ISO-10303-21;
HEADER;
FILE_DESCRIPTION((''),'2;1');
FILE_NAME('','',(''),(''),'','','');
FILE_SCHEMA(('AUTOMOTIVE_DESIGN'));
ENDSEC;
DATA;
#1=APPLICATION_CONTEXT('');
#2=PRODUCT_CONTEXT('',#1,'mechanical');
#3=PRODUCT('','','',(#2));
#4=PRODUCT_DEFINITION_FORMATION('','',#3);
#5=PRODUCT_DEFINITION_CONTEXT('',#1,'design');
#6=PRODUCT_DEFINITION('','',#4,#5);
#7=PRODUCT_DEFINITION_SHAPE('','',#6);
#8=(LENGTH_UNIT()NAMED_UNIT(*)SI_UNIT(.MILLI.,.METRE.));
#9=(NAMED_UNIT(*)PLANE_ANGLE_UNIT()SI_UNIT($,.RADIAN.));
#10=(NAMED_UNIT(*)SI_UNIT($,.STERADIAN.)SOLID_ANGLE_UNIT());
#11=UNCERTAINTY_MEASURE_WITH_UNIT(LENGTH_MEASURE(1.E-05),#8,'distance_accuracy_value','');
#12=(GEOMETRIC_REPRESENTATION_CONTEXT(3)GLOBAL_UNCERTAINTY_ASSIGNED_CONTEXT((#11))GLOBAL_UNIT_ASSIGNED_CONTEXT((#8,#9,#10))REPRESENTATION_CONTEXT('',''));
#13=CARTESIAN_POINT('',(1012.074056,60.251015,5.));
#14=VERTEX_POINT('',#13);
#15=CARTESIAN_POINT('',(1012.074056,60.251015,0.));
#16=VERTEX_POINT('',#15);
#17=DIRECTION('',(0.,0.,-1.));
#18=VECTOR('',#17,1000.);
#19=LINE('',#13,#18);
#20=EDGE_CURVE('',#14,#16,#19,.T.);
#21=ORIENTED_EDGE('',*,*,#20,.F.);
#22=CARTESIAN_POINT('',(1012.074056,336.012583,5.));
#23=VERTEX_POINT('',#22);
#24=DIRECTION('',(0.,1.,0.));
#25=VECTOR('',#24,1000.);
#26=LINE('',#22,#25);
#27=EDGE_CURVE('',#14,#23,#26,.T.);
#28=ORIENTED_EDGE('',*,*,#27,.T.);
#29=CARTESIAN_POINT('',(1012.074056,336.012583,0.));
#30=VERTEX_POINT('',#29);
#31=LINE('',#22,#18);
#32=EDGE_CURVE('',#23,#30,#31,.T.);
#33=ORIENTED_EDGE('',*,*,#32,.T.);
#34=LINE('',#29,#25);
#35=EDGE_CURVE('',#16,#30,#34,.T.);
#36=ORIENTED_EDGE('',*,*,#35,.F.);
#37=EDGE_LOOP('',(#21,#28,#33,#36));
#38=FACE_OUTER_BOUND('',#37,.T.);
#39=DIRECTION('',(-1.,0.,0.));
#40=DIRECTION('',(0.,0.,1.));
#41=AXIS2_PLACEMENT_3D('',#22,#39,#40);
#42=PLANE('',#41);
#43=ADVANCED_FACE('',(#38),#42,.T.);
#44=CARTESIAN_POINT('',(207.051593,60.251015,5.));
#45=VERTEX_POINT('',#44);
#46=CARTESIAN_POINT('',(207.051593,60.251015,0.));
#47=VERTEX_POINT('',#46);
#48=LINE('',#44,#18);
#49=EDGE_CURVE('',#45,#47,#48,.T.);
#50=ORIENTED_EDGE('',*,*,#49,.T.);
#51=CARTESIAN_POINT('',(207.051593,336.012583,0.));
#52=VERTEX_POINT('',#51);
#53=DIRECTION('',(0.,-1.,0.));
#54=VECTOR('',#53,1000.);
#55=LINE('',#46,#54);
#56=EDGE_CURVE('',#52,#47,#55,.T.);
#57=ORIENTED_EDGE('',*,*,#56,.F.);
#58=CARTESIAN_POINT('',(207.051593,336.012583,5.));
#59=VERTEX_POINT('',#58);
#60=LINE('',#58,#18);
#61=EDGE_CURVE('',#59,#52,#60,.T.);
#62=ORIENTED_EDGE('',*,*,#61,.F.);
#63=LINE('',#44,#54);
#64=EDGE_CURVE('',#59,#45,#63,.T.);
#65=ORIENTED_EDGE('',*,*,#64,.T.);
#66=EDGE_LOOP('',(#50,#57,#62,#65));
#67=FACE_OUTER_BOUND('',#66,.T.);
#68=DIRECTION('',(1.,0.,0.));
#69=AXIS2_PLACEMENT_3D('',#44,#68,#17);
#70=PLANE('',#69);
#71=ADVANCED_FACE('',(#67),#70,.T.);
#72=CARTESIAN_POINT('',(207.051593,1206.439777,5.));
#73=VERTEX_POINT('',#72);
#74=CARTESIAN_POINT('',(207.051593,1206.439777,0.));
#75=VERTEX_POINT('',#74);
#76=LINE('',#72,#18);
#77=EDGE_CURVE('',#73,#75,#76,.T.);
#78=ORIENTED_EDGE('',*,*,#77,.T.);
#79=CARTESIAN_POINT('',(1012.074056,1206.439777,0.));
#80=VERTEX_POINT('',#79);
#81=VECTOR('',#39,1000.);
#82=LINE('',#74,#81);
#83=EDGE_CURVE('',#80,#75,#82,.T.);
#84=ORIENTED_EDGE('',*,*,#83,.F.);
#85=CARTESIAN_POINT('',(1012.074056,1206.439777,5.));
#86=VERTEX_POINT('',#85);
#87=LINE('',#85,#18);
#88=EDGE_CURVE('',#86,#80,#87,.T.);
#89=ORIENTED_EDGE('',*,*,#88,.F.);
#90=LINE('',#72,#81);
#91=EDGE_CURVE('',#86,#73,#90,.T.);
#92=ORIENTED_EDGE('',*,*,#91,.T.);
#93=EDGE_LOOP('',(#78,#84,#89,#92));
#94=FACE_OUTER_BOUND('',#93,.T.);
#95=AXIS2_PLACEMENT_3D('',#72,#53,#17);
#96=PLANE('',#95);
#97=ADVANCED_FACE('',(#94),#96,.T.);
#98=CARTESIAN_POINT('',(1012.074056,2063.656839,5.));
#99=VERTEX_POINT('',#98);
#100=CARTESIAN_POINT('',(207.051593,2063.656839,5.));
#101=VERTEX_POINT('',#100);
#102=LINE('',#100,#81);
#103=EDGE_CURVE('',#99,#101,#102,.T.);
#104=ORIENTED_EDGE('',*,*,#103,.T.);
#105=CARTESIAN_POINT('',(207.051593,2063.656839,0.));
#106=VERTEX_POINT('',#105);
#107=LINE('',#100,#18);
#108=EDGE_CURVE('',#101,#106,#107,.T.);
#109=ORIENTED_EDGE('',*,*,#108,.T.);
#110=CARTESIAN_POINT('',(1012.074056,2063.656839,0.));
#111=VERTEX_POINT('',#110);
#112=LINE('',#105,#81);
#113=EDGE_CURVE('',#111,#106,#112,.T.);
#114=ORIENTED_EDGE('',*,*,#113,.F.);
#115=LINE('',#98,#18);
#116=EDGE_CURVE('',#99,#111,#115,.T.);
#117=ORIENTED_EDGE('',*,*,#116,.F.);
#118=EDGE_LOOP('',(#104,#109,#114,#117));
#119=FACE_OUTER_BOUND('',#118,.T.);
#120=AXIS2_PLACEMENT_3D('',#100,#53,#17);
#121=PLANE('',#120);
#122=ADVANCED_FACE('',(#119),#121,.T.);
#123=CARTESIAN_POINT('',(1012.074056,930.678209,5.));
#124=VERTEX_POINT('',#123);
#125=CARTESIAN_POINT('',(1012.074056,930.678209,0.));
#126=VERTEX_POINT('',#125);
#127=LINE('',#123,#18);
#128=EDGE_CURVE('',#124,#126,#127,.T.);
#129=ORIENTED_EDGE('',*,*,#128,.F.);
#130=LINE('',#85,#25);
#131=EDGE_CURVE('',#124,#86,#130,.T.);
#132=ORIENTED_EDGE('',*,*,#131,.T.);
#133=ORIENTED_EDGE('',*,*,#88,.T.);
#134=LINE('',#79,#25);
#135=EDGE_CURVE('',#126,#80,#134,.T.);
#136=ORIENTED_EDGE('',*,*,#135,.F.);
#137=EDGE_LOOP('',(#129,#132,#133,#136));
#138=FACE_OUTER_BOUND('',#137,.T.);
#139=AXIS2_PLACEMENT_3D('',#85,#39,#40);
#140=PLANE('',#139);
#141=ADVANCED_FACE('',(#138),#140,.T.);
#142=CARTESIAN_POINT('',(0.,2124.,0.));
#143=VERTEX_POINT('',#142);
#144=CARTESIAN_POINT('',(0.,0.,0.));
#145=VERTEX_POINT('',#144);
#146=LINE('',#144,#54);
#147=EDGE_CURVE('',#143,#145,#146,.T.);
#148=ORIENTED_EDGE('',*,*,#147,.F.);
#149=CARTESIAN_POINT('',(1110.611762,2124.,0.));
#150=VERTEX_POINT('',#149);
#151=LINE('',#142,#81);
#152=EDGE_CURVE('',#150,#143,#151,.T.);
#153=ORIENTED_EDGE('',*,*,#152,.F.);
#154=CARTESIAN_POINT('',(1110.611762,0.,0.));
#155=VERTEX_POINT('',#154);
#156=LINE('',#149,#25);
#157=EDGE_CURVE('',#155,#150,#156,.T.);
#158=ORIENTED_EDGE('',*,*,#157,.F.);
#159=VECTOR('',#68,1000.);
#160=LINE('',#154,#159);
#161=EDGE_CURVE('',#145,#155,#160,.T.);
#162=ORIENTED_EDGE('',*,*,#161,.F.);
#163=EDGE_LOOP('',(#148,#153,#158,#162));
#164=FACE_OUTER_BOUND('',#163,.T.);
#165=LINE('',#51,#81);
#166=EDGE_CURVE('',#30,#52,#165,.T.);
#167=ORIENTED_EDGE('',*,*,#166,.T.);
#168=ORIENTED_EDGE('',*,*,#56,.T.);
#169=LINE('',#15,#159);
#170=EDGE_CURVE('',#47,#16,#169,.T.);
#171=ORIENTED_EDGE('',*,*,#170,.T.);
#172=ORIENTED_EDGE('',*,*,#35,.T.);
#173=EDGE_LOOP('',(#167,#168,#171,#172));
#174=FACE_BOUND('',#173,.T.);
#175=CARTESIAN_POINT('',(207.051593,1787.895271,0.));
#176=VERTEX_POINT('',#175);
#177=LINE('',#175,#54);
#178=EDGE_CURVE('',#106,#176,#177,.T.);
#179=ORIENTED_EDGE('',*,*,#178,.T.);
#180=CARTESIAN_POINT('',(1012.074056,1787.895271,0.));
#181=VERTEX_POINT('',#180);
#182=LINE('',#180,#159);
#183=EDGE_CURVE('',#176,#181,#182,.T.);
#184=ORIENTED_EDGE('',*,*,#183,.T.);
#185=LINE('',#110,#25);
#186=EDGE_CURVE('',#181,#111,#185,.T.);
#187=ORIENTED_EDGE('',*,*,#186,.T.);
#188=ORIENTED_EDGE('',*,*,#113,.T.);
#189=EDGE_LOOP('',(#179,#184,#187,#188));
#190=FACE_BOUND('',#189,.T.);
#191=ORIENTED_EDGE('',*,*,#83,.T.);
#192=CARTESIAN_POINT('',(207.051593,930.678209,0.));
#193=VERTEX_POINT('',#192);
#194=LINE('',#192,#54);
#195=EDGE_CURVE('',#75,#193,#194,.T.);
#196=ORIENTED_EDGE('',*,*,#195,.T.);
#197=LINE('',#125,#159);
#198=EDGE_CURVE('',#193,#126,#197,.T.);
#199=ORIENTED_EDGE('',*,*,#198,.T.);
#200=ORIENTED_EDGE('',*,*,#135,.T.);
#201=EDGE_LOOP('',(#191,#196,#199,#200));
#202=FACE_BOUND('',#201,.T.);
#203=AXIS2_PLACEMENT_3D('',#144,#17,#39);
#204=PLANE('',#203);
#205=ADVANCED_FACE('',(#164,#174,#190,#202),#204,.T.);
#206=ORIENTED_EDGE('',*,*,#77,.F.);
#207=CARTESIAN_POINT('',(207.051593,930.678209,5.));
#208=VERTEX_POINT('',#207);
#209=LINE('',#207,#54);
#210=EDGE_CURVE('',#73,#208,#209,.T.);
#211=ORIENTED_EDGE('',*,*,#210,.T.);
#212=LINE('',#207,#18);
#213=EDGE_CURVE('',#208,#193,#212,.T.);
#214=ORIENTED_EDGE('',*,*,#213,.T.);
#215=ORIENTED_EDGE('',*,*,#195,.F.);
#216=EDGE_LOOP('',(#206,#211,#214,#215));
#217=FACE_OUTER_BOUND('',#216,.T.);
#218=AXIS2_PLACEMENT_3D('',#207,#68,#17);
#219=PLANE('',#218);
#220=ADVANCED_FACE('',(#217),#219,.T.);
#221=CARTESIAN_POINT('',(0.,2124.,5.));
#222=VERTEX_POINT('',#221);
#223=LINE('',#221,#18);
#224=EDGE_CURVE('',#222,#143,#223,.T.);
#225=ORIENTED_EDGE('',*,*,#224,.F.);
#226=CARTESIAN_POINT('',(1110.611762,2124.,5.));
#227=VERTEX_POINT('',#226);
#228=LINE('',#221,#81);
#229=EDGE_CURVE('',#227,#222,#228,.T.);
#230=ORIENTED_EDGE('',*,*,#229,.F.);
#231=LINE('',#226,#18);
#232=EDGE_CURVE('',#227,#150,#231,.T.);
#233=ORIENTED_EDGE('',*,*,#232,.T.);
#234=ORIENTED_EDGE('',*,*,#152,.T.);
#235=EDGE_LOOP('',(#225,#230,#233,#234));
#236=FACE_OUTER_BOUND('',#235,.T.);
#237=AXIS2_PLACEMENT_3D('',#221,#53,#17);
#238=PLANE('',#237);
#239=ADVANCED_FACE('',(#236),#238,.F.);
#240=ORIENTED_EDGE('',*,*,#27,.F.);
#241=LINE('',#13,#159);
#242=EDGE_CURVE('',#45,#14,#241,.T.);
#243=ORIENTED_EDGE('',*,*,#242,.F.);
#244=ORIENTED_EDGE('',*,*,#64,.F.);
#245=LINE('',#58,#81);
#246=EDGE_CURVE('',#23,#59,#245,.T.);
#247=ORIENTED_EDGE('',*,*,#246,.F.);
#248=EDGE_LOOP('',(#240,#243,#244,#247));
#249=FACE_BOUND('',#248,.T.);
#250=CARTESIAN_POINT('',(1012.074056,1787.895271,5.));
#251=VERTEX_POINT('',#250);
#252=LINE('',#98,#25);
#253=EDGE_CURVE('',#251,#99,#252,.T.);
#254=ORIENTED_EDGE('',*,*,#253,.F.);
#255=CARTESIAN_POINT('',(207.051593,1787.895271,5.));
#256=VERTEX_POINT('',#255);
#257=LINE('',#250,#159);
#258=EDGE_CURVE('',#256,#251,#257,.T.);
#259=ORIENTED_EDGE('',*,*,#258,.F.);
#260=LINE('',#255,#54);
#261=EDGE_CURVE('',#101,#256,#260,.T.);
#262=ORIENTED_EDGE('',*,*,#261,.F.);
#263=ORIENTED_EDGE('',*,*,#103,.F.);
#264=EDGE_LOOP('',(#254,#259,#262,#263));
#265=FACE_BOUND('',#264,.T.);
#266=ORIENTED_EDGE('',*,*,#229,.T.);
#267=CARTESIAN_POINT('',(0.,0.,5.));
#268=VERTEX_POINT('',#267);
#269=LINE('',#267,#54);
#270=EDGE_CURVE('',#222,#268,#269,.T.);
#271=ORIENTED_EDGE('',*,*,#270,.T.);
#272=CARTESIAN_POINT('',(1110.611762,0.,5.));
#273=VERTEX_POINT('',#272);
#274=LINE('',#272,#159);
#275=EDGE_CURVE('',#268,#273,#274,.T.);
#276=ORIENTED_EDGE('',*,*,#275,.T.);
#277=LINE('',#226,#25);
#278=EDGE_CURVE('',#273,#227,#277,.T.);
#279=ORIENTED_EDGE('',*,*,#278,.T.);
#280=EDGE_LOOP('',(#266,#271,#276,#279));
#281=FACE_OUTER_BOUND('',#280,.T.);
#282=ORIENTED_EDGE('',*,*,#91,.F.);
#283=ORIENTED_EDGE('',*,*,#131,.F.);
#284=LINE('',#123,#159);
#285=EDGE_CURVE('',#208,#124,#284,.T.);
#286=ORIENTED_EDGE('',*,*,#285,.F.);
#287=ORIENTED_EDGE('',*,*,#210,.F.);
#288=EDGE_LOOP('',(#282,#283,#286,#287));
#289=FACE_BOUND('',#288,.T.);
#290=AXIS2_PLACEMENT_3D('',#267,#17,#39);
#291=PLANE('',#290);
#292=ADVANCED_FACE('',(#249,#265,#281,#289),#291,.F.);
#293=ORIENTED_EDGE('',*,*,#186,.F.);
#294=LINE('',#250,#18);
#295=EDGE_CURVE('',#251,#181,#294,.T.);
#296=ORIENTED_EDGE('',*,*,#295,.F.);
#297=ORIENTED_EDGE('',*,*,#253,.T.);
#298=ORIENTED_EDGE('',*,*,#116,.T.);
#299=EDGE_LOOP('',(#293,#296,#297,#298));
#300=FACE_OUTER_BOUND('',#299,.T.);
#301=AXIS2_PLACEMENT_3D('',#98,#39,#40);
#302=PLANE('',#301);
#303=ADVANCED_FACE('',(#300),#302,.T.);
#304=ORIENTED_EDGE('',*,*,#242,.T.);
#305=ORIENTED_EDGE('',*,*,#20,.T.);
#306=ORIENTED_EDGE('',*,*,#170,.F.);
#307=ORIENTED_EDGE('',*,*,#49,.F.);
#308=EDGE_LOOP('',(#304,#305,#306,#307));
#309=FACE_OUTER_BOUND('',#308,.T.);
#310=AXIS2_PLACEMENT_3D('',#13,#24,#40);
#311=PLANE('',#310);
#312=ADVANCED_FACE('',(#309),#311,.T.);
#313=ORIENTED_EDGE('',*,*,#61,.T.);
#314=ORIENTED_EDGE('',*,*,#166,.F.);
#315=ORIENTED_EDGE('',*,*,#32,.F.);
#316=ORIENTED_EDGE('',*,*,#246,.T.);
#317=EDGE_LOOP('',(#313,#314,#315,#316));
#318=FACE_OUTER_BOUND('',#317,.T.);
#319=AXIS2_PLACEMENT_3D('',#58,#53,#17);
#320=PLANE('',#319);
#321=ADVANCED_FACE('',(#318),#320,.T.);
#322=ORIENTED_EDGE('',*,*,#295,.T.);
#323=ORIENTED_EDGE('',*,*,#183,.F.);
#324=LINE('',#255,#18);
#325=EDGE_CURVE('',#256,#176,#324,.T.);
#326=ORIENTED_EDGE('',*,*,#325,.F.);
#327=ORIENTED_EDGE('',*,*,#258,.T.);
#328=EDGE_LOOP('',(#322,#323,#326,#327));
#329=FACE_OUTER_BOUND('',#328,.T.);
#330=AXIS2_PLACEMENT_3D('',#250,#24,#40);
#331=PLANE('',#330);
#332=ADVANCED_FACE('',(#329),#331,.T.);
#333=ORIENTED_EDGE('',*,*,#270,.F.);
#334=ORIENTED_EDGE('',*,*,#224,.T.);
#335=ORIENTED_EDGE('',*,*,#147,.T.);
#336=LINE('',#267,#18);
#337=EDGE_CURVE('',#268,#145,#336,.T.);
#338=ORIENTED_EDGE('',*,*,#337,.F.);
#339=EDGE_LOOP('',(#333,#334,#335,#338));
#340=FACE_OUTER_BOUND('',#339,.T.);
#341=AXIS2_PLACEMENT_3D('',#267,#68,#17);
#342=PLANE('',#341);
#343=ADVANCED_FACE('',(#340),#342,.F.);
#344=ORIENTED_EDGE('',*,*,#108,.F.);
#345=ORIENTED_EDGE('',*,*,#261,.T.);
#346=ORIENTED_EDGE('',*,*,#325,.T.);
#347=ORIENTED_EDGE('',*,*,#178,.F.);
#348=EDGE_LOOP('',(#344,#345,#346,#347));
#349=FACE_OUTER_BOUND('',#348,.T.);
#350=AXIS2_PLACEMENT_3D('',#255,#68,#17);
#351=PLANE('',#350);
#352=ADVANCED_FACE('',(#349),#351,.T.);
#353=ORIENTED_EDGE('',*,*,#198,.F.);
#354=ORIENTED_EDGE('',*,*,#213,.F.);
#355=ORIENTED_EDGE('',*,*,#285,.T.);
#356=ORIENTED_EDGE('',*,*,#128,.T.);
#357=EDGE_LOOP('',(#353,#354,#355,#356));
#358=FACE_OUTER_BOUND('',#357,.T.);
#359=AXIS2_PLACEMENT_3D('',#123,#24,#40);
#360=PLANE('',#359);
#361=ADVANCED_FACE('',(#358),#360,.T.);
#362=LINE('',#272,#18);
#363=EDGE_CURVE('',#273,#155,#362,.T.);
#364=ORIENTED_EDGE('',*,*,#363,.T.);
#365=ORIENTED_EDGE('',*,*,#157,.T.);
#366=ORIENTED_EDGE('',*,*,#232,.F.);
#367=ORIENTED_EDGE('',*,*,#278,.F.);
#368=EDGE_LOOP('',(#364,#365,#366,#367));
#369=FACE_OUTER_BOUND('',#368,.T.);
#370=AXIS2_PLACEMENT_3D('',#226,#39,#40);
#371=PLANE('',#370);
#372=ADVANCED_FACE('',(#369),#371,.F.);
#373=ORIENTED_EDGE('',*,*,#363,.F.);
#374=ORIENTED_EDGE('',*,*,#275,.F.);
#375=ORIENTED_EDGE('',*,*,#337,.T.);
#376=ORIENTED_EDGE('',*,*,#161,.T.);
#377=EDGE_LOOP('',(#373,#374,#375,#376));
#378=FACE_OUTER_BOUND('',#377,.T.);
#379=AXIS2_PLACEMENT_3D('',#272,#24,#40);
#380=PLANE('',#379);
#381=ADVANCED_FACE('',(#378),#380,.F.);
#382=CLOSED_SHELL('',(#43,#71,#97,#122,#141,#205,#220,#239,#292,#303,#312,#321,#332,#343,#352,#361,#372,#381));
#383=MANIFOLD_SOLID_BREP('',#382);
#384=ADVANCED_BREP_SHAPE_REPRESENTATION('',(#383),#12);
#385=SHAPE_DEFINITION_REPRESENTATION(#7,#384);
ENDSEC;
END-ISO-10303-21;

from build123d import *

# Parameters (mm, degrees)
SKETCH1_W           = 1110.611762236
SKETCH1_H           = 2124
SKETCH1_W_2         = 805.022462921
SKETCH1_H_2         = 275.761568038
BOSS_EXTRUDE1_DEPTH = 5


with BuildPart() as part:
    # Sketch1 → Boss-Extrude1 (new body)
    with BuildSketch(Plane.XY):
        with Locations((555.305881118, 1062)):
            Rectangle(SKETCH1_W, SKETCH1_H)
        with Locations((609.562824722, 1925.776054905)):
            Rectangle(SKETCH1_W_2, SKETCH1_H_2, mode=Mode.SUBTRACT)
        with Locations((609.562824722, 1068.55899332)):
            Rectangle(SKETCH1_W_2, SKETCH1_H_2, mode=Mode.SUBTRACT)
        with Locations((609.562824722, 198.131798559)):
            Rectangle(SKETCH1_W_2, SKETCH1_H_2, mode=Mode.SUBTRACT)
    extrude(amount=BOSS_EXTRUDE1_DEPTH)


solid = part.part
